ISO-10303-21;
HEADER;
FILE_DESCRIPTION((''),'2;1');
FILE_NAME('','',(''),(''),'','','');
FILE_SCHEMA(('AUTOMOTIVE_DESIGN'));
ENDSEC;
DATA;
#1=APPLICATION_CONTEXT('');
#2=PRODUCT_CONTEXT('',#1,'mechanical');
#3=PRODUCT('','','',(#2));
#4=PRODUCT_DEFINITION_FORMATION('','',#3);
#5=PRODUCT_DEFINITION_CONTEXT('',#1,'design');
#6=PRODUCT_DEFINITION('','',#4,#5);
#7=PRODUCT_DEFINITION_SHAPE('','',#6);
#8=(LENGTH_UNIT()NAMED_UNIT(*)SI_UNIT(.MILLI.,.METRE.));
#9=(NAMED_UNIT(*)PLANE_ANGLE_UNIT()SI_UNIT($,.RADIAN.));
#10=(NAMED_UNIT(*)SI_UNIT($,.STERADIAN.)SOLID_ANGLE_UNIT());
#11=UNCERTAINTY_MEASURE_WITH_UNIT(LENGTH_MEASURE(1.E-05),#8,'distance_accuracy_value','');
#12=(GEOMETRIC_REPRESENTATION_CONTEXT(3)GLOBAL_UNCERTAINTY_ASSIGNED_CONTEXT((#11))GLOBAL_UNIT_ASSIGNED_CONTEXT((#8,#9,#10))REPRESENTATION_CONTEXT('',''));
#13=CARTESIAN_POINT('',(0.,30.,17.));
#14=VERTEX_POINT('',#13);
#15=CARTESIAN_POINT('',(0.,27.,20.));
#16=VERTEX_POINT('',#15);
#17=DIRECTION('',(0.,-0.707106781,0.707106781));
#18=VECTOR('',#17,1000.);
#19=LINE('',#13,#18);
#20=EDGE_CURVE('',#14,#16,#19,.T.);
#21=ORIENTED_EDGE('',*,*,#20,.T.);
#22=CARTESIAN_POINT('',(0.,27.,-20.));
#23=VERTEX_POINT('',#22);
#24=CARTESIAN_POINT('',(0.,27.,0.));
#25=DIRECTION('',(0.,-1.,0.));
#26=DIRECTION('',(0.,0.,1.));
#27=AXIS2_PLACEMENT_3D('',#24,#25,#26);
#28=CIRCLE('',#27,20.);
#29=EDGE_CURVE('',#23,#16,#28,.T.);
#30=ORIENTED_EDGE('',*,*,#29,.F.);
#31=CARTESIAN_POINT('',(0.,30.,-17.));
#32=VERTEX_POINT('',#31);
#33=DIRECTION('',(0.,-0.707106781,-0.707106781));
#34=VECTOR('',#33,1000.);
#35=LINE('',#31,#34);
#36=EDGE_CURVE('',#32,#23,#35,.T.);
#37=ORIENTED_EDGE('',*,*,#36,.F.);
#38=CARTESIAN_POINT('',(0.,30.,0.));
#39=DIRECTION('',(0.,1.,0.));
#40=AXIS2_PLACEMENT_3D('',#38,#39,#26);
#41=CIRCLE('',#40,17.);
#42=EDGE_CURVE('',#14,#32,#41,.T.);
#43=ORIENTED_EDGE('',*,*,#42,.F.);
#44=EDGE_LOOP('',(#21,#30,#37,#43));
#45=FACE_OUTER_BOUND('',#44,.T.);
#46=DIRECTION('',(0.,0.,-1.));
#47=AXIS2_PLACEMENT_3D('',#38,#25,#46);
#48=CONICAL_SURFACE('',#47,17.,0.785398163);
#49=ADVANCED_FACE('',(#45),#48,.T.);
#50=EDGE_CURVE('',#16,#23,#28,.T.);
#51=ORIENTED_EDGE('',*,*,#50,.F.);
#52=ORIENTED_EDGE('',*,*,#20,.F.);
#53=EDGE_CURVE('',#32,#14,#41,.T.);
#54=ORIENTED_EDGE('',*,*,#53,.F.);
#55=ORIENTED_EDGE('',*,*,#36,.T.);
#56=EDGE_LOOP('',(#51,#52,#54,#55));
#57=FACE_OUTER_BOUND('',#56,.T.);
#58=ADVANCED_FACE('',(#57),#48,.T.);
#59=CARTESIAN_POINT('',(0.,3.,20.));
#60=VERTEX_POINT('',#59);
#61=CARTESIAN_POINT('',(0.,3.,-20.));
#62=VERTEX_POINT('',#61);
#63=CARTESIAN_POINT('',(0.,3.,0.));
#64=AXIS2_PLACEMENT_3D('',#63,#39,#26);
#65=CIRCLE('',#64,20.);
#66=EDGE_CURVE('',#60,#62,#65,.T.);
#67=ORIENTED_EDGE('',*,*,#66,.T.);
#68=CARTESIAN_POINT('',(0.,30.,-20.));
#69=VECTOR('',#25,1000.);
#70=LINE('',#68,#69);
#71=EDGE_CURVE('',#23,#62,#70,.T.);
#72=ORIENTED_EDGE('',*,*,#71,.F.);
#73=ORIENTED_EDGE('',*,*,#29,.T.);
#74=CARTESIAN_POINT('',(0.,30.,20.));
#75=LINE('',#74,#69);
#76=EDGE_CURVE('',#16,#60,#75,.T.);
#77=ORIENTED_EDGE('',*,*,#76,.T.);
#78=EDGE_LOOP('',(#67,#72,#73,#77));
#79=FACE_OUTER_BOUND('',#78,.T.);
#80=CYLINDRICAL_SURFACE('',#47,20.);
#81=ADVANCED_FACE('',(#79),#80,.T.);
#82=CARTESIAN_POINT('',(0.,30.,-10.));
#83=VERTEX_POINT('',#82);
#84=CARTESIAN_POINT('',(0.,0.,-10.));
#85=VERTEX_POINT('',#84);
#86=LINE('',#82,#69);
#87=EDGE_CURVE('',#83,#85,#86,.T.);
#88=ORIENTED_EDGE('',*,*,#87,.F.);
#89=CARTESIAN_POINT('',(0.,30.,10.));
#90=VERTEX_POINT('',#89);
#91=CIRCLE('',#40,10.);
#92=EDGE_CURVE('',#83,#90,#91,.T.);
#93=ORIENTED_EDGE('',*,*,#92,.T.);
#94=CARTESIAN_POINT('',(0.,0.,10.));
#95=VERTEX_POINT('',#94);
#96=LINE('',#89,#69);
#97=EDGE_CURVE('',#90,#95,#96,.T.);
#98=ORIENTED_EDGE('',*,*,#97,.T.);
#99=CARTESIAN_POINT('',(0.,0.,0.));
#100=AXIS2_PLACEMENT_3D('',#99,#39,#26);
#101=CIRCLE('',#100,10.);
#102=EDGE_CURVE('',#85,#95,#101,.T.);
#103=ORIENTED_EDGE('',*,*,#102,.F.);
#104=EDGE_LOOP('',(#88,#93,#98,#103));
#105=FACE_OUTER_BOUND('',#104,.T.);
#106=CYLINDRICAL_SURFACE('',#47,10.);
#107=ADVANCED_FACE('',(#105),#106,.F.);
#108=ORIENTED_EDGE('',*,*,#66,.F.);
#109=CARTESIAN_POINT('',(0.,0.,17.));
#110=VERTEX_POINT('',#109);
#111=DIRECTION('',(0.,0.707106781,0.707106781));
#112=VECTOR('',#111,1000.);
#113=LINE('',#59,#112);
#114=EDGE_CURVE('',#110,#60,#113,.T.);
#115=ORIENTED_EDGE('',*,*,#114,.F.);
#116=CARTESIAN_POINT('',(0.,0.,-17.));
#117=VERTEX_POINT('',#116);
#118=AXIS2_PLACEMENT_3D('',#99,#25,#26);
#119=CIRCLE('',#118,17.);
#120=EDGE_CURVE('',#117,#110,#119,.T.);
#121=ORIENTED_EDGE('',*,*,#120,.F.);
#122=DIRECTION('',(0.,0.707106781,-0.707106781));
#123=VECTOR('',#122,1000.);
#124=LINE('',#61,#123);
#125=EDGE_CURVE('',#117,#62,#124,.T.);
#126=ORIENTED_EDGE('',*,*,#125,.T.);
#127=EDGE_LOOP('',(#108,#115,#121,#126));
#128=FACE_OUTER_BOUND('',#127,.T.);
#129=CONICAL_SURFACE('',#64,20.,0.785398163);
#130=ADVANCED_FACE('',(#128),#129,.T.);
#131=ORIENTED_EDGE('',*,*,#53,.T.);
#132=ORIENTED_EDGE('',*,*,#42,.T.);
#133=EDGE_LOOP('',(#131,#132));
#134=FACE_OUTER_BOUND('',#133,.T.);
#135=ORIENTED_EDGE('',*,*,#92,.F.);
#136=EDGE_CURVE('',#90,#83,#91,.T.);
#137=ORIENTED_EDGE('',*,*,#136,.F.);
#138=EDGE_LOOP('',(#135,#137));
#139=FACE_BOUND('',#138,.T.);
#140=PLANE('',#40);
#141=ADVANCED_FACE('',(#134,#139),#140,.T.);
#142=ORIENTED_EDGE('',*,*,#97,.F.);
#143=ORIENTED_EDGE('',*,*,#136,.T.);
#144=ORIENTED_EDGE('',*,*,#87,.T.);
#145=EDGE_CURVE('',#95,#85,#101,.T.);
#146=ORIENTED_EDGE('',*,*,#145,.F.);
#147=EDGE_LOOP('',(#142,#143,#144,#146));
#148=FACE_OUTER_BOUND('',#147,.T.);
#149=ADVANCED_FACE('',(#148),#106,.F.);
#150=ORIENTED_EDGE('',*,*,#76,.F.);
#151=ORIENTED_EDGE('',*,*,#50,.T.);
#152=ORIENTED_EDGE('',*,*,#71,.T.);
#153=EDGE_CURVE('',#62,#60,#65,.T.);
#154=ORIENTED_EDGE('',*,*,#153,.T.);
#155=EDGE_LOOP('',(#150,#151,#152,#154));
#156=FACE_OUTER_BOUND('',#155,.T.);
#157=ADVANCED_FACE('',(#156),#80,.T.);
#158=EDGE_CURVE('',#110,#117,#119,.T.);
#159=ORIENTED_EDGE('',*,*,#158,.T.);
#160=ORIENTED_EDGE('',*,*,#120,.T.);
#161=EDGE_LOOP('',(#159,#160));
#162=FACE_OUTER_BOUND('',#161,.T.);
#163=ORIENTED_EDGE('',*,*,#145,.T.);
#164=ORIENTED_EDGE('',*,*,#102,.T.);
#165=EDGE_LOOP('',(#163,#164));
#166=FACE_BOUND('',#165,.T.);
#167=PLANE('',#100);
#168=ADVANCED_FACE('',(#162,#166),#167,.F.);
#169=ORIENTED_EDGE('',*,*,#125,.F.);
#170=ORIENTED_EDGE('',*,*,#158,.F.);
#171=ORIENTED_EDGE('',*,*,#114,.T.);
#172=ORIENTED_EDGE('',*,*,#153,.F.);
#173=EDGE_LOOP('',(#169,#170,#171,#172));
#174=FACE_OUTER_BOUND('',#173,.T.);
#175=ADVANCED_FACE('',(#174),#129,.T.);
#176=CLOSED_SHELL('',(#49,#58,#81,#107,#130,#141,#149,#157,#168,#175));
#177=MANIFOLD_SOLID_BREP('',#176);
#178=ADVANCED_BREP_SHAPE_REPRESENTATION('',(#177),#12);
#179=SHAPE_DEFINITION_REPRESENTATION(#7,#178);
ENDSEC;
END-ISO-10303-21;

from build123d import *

# Parameters (mm, degrees)
SKETCH1_R           = 20
SKETCH1_R_2         = 10
BOSS_EXTRUDE1_DEPTH = 30
CHAMFER1_SIZE       = 3


with BuildPart() as part:
    # Sketch1 → Boss-Extrude1 (new body)
    with BuildSketch(Plane(origin=(0, 0, 0), x_dir=(1, 0, 0), z_dir=(0, 1, 0))):
        with Locations(Location((0, 0, 0), (0, 0, 270))):
            Circle(SKETCH1_R)
        with Locations(Location((0, 0, 0), (0, 0, 270))):
            Circle(SKETCH1_R_2, mode=Mode.SUBTRACT)
    extrude(amount=BOSS_EXTRUDE1_DEPTH)

    # Chamfer1
    chamfer1_edges = [part.edges().sort_by_distance(p)[0] for p in [
        (0, 0, -20),
        (0, 30, -20),
    ]]
    chamfer(chamfer1_edges, length=CHAMFER1_SIZE)


solid = part.part
